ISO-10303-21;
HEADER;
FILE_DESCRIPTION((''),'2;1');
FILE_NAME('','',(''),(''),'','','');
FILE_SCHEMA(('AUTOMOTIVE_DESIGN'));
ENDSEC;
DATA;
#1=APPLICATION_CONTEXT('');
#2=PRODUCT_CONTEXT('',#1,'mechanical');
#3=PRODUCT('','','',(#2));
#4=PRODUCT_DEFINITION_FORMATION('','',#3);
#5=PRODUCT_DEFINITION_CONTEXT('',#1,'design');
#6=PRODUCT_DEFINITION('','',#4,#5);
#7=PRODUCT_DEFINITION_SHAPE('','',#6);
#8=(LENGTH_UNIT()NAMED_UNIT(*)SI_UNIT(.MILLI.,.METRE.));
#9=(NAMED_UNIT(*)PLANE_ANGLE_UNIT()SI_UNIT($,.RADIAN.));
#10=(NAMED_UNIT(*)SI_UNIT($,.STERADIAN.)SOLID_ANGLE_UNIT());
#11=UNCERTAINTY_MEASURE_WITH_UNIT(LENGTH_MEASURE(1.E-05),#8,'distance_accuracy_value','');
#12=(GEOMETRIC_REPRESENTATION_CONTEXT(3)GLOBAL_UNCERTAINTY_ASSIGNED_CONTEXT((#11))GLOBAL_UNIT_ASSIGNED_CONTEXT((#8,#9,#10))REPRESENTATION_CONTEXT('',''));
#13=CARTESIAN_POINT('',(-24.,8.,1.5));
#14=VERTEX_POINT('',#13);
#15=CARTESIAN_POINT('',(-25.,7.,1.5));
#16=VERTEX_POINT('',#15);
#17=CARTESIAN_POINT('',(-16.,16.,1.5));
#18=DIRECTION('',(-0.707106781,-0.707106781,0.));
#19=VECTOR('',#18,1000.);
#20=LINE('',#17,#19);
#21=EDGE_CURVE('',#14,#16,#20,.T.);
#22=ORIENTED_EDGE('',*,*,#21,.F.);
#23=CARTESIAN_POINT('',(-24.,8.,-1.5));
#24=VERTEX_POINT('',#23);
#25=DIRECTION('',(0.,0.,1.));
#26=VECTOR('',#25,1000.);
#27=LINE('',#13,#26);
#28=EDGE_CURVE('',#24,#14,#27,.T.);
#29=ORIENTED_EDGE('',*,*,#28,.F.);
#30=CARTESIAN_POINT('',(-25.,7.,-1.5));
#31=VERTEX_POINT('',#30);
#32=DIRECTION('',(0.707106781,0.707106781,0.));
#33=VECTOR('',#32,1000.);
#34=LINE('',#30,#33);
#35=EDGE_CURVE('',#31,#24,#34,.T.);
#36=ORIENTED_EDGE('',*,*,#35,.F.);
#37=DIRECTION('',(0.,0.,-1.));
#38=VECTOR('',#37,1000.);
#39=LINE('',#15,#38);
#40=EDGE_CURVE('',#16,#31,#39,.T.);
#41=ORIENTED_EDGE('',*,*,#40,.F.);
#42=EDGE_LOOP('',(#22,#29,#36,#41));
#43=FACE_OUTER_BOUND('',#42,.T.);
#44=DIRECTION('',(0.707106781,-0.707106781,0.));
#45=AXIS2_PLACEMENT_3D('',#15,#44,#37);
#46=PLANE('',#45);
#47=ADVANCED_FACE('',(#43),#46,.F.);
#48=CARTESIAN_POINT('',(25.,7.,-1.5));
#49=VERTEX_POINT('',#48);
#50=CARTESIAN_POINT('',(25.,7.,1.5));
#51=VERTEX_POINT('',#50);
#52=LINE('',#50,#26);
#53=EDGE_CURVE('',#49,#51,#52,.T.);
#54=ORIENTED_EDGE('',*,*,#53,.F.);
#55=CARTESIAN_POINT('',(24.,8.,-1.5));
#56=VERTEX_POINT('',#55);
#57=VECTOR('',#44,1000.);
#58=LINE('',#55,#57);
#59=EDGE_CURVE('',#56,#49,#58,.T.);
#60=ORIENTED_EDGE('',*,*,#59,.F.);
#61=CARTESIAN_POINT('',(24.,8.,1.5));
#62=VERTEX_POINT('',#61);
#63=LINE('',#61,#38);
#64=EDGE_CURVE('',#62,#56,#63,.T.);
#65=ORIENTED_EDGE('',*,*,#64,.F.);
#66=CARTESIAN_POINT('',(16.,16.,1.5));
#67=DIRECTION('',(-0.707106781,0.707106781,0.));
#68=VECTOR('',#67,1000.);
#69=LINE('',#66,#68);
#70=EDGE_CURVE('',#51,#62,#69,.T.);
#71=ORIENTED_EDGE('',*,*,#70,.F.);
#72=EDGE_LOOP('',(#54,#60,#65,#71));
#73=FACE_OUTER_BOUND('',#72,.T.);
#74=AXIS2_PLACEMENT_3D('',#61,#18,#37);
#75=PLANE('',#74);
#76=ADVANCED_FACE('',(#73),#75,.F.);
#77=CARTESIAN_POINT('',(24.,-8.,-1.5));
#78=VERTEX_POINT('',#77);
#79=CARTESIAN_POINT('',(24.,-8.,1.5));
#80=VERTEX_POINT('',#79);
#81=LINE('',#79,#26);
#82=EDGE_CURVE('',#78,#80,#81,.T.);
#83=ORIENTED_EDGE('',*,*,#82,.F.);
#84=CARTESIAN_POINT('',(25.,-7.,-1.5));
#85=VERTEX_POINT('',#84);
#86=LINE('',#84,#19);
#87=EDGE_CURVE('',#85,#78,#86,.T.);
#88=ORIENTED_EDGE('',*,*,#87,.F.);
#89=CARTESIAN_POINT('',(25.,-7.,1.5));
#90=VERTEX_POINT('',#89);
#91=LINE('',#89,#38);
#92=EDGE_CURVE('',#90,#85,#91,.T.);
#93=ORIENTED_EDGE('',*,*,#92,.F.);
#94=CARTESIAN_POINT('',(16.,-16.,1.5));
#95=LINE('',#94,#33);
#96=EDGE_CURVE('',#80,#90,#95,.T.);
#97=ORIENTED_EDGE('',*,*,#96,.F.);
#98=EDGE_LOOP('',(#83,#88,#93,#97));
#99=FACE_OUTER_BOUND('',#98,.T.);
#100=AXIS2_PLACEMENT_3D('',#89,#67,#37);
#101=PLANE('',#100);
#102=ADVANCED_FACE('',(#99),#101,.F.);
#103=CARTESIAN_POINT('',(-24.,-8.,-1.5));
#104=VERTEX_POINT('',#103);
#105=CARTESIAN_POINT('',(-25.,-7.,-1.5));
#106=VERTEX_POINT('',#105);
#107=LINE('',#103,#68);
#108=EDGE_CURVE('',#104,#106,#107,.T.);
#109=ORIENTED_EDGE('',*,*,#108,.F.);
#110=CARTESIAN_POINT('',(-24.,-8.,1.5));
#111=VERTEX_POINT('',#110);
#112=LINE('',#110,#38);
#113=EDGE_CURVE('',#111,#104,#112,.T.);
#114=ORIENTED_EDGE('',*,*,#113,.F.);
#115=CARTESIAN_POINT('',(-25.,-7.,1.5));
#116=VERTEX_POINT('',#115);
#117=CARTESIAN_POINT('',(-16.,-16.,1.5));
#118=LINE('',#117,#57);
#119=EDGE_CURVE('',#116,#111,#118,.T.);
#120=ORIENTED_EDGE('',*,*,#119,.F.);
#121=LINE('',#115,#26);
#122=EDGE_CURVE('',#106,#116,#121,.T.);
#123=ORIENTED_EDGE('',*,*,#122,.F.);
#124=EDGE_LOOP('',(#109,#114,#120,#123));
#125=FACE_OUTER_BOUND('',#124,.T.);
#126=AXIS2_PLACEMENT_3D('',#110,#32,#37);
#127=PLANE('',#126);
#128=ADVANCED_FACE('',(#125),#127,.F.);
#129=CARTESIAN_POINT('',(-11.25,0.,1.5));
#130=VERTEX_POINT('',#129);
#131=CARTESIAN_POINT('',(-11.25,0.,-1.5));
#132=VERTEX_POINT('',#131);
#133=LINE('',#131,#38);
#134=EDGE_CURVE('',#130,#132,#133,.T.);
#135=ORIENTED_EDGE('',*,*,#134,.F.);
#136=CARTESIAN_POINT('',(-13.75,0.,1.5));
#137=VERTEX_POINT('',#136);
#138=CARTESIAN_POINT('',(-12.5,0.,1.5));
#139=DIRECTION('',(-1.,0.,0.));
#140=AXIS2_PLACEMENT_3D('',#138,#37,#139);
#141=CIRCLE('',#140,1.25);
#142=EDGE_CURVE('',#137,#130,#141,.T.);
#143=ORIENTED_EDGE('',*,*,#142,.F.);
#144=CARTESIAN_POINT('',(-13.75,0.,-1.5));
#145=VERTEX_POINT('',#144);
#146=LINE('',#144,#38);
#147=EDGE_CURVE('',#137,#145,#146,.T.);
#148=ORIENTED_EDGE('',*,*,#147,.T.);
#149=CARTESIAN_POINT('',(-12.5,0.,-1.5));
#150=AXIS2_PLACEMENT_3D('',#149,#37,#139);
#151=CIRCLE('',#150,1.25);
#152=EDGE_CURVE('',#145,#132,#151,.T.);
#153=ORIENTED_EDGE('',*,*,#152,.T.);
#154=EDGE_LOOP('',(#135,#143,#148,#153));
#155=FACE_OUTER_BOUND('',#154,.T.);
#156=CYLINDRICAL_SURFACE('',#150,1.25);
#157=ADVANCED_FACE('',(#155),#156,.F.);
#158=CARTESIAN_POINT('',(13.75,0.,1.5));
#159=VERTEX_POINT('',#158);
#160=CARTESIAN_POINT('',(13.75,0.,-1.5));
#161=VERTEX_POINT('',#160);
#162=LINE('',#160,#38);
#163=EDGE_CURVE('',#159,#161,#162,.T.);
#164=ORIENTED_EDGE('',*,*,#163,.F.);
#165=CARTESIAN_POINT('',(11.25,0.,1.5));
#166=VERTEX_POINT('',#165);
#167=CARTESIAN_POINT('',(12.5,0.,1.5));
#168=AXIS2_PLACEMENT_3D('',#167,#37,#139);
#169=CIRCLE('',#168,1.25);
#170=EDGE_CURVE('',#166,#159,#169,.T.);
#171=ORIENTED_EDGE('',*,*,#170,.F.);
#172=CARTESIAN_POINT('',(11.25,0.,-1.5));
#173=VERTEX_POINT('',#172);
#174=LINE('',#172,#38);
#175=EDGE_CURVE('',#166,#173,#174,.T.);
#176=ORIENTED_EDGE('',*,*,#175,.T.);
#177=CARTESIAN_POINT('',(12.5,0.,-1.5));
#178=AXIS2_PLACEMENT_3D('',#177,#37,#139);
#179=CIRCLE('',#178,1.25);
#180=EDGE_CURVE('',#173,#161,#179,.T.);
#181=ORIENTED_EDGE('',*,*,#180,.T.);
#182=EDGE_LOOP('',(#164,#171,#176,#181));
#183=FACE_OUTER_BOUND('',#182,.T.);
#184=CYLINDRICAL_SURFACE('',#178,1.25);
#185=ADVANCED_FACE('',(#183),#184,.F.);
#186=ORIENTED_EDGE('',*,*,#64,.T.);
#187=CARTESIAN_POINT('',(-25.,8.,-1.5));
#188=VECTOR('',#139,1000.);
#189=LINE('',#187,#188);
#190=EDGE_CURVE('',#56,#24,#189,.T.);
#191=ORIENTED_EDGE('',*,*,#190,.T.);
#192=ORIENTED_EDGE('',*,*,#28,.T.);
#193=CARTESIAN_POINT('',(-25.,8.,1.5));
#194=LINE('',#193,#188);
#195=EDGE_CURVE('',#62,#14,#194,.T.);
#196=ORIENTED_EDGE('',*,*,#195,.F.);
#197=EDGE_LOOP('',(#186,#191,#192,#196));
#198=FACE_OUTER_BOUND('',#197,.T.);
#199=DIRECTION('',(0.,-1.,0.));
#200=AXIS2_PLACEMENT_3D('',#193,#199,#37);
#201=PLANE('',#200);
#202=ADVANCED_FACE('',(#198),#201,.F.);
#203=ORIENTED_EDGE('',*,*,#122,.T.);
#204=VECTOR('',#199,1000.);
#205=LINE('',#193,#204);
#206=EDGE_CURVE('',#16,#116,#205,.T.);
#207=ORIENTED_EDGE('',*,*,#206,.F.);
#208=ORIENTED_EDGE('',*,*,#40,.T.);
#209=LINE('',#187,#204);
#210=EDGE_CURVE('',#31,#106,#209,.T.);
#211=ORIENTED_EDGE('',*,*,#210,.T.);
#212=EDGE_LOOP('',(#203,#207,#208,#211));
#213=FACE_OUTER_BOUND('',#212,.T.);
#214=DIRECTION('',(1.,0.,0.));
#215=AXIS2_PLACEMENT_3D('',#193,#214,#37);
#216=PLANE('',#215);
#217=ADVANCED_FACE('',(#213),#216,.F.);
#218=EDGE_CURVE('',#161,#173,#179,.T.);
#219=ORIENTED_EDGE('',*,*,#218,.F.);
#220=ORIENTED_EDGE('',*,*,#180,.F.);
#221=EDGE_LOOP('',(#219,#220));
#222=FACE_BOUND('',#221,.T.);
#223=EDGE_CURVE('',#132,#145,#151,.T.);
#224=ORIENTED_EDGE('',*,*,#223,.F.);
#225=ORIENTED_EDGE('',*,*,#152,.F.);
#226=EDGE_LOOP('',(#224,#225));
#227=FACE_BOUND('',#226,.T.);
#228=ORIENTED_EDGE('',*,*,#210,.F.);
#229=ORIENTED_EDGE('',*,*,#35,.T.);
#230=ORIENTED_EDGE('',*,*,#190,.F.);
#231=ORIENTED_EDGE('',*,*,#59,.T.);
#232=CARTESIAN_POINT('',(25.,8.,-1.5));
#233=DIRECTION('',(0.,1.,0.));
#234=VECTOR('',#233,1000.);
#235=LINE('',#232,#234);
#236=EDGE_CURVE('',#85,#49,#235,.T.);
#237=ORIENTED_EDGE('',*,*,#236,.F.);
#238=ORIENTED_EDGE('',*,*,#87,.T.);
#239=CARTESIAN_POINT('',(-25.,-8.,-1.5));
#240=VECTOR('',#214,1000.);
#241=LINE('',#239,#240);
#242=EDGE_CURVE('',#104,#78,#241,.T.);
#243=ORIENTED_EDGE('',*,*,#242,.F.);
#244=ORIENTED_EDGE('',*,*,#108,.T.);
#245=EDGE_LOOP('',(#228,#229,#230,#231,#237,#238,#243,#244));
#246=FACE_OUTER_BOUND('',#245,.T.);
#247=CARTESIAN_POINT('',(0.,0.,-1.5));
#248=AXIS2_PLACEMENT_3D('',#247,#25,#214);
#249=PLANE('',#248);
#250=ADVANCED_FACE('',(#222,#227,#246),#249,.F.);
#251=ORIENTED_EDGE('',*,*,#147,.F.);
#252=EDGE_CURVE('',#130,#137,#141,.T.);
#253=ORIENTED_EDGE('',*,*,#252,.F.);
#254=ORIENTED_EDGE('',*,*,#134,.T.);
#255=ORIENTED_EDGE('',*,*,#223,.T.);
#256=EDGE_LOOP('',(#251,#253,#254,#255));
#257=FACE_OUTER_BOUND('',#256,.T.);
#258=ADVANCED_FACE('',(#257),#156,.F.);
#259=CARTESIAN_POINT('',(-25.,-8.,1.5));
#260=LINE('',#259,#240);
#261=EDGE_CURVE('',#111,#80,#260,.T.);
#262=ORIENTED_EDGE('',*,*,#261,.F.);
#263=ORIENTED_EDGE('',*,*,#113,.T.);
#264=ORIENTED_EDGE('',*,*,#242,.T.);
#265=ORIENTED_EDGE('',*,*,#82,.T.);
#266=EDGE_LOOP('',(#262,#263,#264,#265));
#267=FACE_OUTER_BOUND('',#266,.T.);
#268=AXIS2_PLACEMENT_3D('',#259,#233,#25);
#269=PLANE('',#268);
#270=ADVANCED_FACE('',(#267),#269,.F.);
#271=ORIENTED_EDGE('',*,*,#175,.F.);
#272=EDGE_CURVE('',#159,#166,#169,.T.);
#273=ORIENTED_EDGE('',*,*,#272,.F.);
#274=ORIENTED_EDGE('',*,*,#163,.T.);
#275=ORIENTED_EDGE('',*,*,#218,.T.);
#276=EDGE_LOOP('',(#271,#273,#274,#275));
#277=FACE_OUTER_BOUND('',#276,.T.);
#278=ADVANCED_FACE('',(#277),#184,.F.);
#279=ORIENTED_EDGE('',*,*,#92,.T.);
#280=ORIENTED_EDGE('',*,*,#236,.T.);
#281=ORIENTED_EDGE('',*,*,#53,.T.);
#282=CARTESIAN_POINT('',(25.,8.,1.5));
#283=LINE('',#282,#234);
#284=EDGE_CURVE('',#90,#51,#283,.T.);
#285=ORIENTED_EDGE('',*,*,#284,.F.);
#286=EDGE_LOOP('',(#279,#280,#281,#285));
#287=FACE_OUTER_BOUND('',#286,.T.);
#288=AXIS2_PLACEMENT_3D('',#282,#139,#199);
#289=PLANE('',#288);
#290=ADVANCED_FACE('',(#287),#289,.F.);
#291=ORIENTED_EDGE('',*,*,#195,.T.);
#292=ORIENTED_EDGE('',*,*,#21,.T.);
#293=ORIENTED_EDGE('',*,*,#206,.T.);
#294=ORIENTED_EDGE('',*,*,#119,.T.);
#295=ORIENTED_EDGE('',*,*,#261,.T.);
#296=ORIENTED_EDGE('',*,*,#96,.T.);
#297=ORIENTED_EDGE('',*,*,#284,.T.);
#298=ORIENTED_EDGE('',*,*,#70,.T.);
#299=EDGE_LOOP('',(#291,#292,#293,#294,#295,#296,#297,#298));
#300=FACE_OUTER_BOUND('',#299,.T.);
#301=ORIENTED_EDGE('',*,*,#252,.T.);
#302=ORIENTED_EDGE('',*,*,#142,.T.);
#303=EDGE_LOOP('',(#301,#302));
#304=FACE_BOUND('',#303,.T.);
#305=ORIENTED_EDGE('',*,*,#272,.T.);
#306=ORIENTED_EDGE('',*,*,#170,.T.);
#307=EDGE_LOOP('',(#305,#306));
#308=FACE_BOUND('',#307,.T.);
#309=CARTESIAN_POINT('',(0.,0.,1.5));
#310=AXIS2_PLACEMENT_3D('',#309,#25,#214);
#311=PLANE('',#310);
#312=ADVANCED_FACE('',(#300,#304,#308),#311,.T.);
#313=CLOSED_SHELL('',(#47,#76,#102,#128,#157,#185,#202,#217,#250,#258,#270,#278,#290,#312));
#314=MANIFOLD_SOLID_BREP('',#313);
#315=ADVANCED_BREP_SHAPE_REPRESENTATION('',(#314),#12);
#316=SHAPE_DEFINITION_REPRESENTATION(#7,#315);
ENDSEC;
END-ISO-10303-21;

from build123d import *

# Parameters (mm, degrees)
SKETCH_1_W         = 50
SKETCH_1_H         = 16
EXTRUDE_1_DEPTH    = 1.5
HOLE_WIZARD_M3_1_D = 2.5
CHAMFER_1_SIZE     = 1


with BuildPart() as part:
    # 草图1 → 凸台-拉伸1 (new, symmetric)
    with BuildSketch(Plane.XY):
        Rectangle(SKETCH_1_W, SKETCH_1_H)
    extrude(amount=EXTRUDE_1_DEPTH, both=True)

    # M3 螺纹孔1 (through all)
    with Locations(Plane(origin=(0, 0, -1.5), x_dir=(-1, 0, 0), z_dir=(0, 0, -1))):
        with Locations((12.5, 0), (-12.5, 0)):
            Hole(HOLE_WIZARD_M3_1_D / 2)

    # 倒角1
    chamfer_1_edges = [part.edges().sort_by_distance(p)[0] for p in [
        (25, -8, 0),
        (-25, -8, 0),
        (-25, 8, 0),
        (25, 8, 0),
    ]]
    chamfer(chamfer_1_edges, length=CHAMFER_1_SIZE)


solid = part.part
